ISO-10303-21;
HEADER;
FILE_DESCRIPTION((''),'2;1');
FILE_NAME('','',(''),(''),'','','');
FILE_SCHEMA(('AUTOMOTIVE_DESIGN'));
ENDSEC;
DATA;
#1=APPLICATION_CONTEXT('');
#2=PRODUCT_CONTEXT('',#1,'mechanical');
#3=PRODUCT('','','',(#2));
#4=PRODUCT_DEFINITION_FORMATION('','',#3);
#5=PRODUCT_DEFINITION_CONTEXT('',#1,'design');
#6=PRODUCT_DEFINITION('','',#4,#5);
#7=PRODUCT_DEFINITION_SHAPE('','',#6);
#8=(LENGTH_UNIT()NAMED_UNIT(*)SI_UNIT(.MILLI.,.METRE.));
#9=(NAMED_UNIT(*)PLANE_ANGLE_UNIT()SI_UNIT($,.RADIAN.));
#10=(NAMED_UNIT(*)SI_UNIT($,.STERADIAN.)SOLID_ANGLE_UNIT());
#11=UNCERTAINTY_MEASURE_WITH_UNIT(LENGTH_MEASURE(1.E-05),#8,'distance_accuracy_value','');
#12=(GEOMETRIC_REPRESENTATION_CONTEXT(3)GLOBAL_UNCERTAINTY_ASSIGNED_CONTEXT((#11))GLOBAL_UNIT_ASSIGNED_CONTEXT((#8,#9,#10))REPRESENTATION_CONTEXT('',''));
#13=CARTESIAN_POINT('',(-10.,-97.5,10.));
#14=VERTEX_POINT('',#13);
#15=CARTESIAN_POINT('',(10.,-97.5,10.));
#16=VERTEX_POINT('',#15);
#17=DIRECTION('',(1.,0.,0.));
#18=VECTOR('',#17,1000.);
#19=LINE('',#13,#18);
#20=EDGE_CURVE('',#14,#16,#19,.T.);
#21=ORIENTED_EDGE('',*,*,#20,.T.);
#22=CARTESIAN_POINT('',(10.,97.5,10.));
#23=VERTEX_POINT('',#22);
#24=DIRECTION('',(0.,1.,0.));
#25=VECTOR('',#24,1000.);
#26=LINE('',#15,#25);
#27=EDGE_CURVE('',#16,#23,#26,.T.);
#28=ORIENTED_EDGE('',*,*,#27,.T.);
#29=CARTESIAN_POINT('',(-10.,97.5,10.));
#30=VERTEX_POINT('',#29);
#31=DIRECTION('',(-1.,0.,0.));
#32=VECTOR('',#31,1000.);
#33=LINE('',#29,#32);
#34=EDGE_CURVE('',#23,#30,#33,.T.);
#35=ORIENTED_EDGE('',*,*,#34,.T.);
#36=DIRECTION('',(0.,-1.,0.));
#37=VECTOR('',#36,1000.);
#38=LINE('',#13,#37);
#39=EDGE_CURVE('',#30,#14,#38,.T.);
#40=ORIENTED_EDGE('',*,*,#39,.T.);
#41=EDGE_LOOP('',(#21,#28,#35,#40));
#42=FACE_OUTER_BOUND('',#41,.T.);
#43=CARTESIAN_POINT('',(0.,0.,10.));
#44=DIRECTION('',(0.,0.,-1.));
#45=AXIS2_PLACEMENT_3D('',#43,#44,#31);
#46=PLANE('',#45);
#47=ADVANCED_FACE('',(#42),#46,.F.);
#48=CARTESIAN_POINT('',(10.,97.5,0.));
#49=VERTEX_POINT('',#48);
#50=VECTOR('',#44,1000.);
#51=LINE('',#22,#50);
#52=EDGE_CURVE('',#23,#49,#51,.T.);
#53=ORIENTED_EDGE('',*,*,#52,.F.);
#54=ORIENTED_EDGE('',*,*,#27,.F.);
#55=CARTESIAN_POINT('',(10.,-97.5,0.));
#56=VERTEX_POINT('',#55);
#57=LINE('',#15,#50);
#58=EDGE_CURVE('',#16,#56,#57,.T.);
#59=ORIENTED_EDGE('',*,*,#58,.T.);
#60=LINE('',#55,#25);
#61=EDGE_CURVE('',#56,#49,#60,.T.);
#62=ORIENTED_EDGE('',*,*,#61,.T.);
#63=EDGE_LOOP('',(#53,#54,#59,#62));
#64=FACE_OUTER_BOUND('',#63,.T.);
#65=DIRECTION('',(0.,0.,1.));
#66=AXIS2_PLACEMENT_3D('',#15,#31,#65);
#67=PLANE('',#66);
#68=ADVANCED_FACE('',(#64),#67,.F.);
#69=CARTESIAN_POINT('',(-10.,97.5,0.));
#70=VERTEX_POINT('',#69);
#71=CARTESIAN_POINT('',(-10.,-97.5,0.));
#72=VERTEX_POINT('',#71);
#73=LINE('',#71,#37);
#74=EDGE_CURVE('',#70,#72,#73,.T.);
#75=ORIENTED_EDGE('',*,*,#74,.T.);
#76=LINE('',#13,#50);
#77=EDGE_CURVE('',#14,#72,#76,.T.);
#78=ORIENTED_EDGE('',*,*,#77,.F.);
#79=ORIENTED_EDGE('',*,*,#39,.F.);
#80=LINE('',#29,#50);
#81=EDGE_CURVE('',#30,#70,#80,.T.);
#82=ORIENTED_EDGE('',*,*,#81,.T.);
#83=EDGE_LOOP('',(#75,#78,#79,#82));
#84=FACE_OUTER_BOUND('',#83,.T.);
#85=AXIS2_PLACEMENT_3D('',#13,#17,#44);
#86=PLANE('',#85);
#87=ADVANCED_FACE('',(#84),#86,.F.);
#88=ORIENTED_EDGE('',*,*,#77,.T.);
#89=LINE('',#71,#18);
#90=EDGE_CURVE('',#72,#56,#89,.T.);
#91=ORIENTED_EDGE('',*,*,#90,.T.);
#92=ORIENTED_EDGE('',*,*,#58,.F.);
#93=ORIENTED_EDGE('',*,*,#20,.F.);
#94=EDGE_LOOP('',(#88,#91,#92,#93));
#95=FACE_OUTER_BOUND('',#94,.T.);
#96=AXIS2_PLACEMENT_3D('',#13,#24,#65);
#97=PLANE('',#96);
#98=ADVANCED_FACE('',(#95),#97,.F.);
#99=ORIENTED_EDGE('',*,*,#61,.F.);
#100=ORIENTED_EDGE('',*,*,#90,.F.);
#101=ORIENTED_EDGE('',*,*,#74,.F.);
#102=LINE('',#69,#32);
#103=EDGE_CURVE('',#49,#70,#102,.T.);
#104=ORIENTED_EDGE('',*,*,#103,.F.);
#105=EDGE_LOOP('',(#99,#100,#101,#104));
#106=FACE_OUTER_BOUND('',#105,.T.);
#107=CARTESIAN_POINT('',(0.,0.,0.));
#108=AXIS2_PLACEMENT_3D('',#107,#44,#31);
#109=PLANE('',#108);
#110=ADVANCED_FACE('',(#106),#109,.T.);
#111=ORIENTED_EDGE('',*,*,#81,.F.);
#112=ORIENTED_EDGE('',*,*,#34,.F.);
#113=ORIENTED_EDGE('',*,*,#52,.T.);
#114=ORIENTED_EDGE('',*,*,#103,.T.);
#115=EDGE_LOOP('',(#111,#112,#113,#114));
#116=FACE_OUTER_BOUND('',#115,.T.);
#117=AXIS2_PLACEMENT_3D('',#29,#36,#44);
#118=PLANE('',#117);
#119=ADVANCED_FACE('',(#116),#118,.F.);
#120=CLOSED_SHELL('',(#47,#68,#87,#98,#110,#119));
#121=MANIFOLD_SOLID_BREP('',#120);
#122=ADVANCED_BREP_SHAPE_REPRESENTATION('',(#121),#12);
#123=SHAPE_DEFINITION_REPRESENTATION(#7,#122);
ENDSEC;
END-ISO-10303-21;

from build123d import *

# Parameters (mm, degrees)
SKETCH_1_W      = 20
SKETCH_1_H      = 195
EXTRUDE_1_DEPTH = 10


with BuildPart() as part:
    # 草图1 → 凸台-拉伸1 (new body)
    with BuildSketch(Plane.XY):
        Rectangle(SKETCH_1_W, SKETCH_1_H)
    extrude(amount=EXTRUDE_1_DEPTH)


solid = part.part
